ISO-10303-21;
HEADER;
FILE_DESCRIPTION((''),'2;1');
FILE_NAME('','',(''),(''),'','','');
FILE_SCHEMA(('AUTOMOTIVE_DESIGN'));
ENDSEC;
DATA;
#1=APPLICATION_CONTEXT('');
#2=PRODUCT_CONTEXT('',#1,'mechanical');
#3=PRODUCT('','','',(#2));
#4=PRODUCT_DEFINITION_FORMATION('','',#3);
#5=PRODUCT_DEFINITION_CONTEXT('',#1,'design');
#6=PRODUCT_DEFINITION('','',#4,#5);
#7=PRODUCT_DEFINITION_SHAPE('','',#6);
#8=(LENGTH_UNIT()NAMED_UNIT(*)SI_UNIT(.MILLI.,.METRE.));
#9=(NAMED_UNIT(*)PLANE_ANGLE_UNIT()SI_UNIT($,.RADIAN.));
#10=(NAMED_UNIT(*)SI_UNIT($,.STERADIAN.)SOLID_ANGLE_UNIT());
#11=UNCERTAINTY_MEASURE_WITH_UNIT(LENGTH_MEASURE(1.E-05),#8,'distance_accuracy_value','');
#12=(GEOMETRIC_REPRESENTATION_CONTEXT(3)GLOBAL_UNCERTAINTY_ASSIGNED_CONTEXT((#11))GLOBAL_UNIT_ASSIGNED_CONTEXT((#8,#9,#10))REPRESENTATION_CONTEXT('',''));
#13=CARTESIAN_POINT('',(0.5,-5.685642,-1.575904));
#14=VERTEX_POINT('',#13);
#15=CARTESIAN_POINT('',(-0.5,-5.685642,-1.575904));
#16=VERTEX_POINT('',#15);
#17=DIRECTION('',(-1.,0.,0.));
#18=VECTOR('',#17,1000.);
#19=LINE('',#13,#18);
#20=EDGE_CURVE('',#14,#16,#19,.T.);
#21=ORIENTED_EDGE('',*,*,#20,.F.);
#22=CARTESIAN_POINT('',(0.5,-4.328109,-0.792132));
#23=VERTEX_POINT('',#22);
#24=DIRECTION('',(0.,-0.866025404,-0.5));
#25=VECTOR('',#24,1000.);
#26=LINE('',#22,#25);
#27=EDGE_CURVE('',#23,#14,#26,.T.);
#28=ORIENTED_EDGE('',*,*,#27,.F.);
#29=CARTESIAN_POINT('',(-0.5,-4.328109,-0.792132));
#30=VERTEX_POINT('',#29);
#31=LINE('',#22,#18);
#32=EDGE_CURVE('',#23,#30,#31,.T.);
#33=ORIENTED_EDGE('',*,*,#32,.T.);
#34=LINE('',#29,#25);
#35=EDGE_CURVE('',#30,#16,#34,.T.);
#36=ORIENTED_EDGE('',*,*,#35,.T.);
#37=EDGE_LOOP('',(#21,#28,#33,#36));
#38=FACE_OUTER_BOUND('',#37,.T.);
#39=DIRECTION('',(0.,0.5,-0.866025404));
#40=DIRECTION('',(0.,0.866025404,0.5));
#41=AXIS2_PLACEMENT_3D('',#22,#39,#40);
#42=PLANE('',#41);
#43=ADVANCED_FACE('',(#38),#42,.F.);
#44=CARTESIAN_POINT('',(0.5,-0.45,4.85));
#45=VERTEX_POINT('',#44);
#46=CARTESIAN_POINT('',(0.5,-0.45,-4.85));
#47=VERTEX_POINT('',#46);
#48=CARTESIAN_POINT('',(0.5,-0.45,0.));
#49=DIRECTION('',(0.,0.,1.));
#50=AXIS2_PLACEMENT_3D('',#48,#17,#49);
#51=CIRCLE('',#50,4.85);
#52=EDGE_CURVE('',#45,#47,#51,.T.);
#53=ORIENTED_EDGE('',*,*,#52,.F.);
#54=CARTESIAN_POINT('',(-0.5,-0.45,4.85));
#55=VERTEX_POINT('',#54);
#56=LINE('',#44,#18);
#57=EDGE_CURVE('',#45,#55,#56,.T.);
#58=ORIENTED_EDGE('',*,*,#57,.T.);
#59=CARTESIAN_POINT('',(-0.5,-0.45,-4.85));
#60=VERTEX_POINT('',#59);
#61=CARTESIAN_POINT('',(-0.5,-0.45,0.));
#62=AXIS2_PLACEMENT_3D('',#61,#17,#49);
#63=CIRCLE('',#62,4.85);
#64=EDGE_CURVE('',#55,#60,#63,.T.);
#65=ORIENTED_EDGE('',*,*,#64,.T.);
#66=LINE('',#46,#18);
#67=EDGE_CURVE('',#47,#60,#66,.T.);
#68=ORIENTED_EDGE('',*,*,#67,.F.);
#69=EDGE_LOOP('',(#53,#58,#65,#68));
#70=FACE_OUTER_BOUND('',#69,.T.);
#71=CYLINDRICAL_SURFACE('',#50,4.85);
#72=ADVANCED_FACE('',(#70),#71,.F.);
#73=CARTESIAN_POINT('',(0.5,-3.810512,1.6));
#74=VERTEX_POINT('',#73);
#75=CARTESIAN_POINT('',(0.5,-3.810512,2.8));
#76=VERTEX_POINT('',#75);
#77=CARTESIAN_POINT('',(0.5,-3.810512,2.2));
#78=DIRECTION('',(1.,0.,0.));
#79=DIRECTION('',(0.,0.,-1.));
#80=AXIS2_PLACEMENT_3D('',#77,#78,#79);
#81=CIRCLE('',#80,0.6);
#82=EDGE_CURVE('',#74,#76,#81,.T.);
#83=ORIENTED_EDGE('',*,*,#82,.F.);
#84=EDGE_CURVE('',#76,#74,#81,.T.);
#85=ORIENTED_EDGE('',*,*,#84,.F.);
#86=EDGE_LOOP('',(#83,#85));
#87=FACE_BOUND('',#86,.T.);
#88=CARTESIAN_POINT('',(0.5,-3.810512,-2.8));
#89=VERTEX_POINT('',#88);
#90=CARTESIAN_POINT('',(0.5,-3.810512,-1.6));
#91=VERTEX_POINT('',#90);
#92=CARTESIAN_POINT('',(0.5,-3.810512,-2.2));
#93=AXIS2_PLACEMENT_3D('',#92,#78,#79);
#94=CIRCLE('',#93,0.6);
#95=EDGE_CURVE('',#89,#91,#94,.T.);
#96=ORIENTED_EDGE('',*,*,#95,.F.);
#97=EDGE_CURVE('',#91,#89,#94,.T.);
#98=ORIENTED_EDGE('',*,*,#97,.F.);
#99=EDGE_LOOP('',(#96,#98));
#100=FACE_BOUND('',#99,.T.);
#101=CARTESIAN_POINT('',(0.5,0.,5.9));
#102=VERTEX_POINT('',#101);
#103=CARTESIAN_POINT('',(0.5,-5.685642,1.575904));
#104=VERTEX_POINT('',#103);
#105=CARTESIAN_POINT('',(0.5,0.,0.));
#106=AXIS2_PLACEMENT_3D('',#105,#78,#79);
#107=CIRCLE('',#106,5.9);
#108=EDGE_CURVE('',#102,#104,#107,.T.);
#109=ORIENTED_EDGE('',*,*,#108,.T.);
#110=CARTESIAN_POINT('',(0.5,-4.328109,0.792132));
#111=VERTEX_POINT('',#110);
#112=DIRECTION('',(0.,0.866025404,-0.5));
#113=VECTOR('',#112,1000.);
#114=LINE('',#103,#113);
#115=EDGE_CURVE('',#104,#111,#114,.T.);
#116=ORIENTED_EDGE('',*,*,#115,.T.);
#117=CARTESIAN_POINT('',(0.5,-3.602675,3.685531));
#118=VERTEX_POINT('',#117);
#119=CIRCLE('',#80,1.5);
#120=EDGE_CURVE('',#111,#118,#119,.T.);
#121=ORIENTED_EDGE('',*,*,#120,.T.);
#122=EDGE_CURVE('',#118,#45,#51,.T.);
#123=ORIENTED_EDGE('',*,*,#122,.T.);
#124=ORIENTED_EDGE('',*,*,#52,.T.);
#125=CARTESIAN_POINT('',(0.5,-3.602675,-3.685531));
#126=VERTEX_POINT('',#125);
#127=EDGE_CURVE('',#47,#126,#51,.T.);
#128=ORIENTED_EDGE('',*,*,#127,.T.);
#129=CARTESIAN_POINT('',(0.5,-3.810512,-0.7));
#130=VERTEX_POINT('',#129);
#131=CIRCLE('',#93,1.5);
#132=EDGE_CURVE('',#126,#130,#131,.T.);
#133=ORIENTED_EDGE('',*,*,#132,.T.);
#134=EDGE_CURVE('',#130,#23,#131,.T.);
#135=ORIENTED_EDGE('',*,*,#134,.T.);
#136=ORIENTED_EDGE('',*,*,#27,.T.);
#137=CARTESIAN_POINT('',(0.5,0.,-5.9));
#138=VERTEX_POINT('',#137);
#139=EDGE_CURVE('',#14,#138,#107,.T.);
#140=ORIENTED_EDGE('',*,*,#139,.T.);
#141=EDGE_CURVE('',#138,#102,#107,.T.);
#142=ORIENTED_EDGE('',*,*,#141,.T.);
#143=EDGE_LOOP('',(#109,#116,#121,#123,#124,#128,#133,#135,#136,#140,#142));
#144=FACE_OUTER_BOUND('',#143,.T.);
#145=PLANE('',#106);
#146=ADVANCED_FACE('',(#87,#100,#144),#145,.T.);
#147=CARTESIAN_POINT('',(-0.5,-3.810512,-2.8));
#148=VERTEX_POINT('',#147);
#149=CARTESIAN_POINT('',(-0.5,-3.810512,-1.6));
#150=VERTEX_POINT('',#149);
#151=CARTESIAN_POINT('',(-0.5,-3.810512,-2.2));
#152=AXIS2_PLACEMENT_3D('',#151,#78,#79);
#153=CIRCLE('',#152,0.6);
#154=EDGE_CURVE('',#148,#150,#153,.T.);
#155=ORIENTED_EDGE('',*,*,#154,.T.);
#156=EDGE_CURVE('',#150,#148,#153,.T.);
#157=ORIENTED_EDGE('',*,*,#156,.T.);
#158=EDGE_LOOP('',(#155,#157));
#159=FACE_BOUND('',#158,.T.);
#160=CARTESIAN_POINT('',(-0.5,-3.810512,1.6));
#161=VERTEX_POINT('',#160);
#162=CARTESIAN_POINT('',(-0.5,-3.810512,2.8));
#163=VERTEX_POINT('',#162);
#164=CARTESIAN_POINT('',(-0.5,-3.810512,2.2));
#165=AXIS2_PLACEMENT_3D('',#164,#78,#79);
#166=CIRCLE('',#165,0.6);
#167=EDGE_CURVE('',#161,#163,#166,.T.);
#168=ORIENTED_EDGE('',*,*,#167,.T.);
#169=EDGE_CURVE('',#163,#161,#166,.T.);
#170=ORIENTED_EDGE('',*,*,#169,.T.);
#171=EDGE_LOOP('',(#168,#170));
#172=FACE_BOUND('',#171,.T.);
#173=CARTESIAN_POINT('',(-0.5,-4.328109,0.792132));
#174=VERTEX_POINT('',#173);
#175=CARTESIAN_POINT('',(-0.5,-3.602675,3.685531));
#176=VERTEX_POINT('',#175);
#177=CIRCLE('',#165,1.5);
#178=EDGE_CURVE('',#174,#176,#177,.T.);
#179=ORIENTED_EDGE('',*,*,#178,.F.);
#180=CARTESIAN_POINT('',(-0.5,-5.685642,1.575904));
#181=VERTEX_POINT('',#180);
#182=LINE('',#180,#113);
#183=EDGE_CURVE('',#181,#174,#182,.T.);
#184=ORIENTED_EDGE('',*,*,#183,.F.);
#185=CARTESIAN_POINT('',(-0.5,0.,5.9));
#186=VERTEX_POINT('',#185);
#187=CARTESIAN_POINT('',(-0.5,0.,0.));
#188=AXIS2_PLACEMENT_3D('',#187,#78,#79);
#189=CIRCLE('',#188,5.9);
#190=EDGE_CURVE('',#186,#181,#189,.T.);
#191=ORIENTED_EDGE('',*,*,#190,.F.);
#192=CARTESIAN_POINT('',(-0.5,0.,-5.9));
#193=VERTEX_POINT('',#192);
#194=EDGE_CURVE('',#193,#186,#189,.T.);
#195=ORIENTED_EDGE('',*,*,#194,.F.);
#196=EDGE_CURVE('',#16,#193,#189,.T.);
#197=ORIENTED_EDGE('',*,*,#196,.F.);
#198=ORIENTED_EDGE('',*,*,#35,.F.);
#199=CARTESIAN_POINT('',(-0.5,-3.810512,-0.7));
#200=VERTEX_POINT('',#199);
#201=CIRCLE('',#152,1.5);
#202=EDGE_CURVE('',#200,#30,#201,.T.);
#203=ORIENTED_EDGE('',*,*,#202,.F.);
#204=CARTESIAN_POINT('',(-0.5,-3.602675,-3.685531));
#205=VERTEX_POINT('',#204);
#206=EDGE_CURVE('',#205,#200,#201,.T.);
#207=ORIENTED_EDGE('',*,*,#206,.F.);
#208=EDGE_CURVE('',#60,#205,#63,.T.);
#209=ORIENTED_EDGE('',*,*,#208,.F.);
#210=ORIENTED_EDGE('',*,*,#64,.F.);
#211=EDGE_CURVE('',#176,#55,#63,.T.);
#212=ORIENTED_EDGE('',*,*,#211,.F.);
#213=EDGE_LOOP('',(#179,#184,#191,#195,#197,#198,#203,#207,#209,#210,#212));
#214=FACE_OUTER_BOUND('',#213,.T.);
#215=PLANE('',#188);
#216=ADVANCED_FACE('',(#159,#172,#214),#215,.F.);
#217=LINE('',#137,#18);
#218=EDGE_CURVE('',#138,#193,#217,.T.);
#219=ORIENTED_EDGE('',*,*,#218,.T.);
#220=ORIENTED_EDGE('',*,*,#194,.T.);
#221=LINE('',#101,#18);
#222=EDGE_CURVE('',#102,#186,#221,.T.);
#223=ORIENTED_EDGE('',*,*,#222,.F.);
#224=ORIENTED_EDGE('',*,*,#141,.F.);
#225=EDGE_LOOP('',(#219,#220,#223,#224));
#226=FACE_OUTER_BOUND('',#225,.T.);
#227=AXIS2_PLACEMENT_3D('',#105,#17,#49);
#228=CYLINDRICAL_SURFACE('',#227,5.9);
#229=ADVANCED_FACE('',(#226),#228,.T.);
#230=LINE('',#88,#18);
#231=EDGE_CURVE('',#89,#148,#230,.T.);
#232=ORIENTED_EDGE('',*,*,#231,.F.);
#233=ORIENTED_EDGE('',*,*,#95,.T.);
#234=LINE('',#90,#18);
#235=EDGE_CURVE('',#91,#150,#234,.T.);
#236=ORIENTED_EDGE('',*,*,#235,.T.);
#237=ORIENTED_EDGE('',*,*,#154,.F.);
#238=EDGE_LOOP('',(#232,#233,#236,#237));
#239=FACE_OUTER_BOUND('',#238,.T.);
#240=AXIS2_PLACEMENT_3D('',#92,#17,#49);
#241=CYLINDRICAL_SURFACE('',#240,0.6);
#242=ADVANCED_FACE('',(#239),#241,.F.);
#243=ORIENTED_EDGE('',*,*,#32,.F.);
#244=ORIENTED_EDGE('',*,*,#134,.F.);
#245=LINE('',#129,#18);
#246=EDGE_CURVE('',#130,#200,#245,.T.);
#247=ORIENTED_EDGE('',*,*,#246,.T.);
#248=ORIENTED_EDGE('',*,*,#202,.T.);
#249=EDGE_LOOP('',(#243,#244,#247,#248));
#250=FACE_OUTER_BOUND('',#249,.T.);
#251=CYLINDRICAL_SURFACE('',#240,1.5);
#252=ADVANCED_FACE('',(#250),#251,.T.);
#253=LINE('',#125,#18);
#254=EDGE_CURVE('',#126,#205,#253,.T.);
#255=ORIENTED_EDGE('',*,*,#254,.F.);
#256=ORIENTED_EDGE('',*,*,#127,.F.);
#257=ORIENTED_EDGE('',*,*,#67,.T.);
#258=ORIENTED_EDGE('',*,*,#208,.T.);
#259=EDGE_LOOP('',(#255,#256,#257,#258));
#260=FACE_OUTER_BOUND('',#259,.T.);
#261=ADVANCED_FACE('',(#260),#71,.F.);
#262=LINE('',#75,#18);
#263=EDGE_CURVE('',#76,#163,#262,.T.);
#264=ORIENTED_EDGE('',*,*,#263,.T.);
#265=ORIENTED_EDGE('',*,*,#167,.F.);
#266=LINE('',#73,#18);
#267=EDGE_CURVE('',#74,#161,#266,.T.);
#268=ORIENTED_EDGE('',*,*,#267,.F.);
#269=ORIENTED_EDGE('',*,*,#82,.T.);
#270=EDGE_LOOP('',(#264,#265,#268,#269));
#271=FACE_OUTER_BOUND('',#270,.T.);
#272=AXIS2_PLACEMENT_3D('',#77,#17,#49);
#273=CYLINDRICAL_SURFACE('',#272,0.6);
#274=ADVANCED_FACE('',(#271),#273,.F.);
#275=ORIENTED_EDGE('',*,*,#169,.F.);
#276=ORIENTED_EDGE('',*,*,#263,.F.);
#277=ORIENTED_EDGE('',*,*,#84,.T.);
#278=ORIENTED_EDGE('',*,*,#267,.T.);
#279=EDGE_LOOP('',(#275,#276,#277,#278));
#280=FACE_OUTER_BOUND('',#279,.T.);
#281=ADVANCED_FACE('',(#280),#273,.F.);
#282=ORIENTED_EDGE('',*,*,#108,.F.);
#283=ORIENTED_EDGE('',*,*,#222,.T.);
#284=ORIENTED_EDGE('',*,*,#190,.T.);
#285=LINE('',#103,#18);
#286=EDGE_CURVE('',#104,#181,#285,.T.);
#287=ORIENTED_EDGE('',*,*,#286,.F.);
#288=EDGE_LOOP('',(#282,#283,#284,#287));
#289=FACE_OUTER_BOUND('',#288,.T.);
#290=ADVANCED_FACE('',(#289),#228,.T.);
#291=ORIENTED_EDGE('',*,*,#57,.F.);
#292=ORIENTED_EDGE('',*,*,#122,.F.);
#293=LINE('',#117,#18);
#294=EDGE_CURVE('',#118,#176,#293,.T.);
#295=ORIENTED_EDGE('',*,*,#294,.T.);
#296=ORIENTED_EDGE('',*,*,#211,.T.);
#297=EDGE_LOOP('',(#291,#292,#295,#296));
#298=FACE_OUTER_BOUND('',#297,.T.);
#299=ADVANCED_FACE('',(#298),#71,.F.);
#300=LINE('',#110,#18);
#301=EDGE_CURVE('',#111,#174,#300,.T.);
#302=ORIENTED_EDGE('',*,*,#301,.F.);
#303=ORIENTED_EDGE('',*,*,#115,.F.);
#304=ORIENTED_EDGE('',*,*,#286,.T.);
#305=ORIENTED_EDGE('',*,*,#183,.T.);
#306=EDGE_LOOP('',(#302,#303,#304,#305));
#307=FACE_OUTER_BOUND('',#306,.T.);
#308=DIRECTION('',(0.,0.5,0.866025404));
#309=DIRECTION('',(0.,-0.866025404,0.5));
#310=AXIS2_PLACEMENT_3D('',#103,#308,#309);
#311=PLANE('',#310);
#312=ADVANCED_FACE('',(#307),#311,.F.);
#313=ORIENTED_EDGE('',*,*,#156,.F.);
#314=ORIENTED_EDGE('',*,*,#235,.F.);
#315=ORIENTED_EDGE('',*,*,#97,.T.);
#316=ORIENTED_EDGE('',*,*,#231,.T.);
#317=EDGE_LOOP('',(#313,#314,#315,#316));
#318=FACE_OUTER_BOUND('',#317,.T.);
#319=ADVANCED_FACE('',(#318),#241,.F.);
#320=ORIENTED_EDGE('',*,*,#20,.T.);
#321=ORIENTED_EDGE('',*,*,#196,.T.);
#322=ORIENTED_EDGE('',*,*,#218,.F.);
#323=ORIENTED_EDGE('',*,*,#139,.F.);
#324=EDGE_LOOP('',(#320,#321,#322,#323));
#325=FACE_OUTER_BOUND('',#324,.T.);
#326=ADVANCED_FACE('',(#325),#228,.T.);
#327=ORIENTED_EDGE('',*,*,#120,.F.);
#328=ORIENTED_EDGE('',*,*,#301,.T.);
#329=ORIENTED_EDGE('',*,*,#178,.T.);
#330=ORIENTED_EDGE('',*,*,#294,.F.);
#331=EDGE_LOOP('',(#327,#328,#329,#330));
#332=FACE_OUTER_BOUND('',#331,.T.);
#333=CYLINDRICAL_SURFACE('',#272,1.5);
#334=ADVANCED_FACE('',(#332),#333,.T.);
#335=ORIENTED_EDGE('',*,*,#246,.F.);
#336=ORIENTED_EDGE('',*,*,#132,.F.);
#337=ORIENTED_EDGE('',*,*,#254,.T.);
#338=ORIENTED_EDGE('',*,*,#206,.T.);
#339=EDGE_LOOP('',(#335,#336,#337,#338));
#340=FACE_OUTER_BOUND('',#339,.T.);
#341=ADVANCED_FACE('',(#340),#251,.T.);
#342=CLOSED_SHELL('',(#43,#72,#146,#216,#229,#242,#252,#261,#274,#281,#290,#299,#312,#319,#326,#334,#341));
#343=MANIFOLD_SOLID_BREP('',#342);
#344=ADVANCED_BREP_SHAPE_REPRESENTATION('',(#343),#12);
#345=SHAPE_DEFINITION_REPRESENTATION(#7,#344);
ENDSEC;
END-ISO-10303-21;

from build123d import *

# Parameters (mm, degrees)
EXTRUDE_1_DEPTH      = 0.5
EXTRUDE_1_DEPTH_BACK = 0.5
SKETCH_1_R           = 0.6


with BuildPart() as part:
    # 草图1 → 凸台-拉伸1 (new, two sides: drawn at the far end of the back side and taken through both)
    with BuildSketch(Plane(origin=(0, 0, 0), x_dir=(0, 0, -1), z_dir=(1, 0, 0)).offset(-EXTRUDE_1_DEPTH_BACK)):
        with BuildLine():
            Line((-1.575903864, -5.685642181), (-0.792131706, -4.328108982))
            ThreePointArc((-0.792131706, -4.328108982), (-1.835210176, -2.355544978), (-3.685531471, -3.602674702))
            ThreePointArc((-3.685531471, -3.602674702), (0, 4.4), (3.685531471, -3.602674702))
            ThreePointArc((3.685531471, -3.602674702), (1.835210176, -2.355544978), (0.792131706, -4.328108982))
            Line((0.792131706, -4.328108982), (1.575903864, -5.685642181))
            ThreePointArc((1.575903864, -5.685642181), (0, 5.9), (-1.575903864, -5.685642181))
        make_face()
        with Locations((2.2, -3.810511777)):
            Circle(SKETCH_1_R, mode=Mode.SUBTRACT)
        with Locations((-2.2, -3.810511777)):
            Circle(SKETCH_1_R, mode=Mode.SUBTRACT)
    extrude(amount=EXTRUDE_1_DEPTH + EXTRUDE_1_DEPTH_BACK)


solid = part.part
